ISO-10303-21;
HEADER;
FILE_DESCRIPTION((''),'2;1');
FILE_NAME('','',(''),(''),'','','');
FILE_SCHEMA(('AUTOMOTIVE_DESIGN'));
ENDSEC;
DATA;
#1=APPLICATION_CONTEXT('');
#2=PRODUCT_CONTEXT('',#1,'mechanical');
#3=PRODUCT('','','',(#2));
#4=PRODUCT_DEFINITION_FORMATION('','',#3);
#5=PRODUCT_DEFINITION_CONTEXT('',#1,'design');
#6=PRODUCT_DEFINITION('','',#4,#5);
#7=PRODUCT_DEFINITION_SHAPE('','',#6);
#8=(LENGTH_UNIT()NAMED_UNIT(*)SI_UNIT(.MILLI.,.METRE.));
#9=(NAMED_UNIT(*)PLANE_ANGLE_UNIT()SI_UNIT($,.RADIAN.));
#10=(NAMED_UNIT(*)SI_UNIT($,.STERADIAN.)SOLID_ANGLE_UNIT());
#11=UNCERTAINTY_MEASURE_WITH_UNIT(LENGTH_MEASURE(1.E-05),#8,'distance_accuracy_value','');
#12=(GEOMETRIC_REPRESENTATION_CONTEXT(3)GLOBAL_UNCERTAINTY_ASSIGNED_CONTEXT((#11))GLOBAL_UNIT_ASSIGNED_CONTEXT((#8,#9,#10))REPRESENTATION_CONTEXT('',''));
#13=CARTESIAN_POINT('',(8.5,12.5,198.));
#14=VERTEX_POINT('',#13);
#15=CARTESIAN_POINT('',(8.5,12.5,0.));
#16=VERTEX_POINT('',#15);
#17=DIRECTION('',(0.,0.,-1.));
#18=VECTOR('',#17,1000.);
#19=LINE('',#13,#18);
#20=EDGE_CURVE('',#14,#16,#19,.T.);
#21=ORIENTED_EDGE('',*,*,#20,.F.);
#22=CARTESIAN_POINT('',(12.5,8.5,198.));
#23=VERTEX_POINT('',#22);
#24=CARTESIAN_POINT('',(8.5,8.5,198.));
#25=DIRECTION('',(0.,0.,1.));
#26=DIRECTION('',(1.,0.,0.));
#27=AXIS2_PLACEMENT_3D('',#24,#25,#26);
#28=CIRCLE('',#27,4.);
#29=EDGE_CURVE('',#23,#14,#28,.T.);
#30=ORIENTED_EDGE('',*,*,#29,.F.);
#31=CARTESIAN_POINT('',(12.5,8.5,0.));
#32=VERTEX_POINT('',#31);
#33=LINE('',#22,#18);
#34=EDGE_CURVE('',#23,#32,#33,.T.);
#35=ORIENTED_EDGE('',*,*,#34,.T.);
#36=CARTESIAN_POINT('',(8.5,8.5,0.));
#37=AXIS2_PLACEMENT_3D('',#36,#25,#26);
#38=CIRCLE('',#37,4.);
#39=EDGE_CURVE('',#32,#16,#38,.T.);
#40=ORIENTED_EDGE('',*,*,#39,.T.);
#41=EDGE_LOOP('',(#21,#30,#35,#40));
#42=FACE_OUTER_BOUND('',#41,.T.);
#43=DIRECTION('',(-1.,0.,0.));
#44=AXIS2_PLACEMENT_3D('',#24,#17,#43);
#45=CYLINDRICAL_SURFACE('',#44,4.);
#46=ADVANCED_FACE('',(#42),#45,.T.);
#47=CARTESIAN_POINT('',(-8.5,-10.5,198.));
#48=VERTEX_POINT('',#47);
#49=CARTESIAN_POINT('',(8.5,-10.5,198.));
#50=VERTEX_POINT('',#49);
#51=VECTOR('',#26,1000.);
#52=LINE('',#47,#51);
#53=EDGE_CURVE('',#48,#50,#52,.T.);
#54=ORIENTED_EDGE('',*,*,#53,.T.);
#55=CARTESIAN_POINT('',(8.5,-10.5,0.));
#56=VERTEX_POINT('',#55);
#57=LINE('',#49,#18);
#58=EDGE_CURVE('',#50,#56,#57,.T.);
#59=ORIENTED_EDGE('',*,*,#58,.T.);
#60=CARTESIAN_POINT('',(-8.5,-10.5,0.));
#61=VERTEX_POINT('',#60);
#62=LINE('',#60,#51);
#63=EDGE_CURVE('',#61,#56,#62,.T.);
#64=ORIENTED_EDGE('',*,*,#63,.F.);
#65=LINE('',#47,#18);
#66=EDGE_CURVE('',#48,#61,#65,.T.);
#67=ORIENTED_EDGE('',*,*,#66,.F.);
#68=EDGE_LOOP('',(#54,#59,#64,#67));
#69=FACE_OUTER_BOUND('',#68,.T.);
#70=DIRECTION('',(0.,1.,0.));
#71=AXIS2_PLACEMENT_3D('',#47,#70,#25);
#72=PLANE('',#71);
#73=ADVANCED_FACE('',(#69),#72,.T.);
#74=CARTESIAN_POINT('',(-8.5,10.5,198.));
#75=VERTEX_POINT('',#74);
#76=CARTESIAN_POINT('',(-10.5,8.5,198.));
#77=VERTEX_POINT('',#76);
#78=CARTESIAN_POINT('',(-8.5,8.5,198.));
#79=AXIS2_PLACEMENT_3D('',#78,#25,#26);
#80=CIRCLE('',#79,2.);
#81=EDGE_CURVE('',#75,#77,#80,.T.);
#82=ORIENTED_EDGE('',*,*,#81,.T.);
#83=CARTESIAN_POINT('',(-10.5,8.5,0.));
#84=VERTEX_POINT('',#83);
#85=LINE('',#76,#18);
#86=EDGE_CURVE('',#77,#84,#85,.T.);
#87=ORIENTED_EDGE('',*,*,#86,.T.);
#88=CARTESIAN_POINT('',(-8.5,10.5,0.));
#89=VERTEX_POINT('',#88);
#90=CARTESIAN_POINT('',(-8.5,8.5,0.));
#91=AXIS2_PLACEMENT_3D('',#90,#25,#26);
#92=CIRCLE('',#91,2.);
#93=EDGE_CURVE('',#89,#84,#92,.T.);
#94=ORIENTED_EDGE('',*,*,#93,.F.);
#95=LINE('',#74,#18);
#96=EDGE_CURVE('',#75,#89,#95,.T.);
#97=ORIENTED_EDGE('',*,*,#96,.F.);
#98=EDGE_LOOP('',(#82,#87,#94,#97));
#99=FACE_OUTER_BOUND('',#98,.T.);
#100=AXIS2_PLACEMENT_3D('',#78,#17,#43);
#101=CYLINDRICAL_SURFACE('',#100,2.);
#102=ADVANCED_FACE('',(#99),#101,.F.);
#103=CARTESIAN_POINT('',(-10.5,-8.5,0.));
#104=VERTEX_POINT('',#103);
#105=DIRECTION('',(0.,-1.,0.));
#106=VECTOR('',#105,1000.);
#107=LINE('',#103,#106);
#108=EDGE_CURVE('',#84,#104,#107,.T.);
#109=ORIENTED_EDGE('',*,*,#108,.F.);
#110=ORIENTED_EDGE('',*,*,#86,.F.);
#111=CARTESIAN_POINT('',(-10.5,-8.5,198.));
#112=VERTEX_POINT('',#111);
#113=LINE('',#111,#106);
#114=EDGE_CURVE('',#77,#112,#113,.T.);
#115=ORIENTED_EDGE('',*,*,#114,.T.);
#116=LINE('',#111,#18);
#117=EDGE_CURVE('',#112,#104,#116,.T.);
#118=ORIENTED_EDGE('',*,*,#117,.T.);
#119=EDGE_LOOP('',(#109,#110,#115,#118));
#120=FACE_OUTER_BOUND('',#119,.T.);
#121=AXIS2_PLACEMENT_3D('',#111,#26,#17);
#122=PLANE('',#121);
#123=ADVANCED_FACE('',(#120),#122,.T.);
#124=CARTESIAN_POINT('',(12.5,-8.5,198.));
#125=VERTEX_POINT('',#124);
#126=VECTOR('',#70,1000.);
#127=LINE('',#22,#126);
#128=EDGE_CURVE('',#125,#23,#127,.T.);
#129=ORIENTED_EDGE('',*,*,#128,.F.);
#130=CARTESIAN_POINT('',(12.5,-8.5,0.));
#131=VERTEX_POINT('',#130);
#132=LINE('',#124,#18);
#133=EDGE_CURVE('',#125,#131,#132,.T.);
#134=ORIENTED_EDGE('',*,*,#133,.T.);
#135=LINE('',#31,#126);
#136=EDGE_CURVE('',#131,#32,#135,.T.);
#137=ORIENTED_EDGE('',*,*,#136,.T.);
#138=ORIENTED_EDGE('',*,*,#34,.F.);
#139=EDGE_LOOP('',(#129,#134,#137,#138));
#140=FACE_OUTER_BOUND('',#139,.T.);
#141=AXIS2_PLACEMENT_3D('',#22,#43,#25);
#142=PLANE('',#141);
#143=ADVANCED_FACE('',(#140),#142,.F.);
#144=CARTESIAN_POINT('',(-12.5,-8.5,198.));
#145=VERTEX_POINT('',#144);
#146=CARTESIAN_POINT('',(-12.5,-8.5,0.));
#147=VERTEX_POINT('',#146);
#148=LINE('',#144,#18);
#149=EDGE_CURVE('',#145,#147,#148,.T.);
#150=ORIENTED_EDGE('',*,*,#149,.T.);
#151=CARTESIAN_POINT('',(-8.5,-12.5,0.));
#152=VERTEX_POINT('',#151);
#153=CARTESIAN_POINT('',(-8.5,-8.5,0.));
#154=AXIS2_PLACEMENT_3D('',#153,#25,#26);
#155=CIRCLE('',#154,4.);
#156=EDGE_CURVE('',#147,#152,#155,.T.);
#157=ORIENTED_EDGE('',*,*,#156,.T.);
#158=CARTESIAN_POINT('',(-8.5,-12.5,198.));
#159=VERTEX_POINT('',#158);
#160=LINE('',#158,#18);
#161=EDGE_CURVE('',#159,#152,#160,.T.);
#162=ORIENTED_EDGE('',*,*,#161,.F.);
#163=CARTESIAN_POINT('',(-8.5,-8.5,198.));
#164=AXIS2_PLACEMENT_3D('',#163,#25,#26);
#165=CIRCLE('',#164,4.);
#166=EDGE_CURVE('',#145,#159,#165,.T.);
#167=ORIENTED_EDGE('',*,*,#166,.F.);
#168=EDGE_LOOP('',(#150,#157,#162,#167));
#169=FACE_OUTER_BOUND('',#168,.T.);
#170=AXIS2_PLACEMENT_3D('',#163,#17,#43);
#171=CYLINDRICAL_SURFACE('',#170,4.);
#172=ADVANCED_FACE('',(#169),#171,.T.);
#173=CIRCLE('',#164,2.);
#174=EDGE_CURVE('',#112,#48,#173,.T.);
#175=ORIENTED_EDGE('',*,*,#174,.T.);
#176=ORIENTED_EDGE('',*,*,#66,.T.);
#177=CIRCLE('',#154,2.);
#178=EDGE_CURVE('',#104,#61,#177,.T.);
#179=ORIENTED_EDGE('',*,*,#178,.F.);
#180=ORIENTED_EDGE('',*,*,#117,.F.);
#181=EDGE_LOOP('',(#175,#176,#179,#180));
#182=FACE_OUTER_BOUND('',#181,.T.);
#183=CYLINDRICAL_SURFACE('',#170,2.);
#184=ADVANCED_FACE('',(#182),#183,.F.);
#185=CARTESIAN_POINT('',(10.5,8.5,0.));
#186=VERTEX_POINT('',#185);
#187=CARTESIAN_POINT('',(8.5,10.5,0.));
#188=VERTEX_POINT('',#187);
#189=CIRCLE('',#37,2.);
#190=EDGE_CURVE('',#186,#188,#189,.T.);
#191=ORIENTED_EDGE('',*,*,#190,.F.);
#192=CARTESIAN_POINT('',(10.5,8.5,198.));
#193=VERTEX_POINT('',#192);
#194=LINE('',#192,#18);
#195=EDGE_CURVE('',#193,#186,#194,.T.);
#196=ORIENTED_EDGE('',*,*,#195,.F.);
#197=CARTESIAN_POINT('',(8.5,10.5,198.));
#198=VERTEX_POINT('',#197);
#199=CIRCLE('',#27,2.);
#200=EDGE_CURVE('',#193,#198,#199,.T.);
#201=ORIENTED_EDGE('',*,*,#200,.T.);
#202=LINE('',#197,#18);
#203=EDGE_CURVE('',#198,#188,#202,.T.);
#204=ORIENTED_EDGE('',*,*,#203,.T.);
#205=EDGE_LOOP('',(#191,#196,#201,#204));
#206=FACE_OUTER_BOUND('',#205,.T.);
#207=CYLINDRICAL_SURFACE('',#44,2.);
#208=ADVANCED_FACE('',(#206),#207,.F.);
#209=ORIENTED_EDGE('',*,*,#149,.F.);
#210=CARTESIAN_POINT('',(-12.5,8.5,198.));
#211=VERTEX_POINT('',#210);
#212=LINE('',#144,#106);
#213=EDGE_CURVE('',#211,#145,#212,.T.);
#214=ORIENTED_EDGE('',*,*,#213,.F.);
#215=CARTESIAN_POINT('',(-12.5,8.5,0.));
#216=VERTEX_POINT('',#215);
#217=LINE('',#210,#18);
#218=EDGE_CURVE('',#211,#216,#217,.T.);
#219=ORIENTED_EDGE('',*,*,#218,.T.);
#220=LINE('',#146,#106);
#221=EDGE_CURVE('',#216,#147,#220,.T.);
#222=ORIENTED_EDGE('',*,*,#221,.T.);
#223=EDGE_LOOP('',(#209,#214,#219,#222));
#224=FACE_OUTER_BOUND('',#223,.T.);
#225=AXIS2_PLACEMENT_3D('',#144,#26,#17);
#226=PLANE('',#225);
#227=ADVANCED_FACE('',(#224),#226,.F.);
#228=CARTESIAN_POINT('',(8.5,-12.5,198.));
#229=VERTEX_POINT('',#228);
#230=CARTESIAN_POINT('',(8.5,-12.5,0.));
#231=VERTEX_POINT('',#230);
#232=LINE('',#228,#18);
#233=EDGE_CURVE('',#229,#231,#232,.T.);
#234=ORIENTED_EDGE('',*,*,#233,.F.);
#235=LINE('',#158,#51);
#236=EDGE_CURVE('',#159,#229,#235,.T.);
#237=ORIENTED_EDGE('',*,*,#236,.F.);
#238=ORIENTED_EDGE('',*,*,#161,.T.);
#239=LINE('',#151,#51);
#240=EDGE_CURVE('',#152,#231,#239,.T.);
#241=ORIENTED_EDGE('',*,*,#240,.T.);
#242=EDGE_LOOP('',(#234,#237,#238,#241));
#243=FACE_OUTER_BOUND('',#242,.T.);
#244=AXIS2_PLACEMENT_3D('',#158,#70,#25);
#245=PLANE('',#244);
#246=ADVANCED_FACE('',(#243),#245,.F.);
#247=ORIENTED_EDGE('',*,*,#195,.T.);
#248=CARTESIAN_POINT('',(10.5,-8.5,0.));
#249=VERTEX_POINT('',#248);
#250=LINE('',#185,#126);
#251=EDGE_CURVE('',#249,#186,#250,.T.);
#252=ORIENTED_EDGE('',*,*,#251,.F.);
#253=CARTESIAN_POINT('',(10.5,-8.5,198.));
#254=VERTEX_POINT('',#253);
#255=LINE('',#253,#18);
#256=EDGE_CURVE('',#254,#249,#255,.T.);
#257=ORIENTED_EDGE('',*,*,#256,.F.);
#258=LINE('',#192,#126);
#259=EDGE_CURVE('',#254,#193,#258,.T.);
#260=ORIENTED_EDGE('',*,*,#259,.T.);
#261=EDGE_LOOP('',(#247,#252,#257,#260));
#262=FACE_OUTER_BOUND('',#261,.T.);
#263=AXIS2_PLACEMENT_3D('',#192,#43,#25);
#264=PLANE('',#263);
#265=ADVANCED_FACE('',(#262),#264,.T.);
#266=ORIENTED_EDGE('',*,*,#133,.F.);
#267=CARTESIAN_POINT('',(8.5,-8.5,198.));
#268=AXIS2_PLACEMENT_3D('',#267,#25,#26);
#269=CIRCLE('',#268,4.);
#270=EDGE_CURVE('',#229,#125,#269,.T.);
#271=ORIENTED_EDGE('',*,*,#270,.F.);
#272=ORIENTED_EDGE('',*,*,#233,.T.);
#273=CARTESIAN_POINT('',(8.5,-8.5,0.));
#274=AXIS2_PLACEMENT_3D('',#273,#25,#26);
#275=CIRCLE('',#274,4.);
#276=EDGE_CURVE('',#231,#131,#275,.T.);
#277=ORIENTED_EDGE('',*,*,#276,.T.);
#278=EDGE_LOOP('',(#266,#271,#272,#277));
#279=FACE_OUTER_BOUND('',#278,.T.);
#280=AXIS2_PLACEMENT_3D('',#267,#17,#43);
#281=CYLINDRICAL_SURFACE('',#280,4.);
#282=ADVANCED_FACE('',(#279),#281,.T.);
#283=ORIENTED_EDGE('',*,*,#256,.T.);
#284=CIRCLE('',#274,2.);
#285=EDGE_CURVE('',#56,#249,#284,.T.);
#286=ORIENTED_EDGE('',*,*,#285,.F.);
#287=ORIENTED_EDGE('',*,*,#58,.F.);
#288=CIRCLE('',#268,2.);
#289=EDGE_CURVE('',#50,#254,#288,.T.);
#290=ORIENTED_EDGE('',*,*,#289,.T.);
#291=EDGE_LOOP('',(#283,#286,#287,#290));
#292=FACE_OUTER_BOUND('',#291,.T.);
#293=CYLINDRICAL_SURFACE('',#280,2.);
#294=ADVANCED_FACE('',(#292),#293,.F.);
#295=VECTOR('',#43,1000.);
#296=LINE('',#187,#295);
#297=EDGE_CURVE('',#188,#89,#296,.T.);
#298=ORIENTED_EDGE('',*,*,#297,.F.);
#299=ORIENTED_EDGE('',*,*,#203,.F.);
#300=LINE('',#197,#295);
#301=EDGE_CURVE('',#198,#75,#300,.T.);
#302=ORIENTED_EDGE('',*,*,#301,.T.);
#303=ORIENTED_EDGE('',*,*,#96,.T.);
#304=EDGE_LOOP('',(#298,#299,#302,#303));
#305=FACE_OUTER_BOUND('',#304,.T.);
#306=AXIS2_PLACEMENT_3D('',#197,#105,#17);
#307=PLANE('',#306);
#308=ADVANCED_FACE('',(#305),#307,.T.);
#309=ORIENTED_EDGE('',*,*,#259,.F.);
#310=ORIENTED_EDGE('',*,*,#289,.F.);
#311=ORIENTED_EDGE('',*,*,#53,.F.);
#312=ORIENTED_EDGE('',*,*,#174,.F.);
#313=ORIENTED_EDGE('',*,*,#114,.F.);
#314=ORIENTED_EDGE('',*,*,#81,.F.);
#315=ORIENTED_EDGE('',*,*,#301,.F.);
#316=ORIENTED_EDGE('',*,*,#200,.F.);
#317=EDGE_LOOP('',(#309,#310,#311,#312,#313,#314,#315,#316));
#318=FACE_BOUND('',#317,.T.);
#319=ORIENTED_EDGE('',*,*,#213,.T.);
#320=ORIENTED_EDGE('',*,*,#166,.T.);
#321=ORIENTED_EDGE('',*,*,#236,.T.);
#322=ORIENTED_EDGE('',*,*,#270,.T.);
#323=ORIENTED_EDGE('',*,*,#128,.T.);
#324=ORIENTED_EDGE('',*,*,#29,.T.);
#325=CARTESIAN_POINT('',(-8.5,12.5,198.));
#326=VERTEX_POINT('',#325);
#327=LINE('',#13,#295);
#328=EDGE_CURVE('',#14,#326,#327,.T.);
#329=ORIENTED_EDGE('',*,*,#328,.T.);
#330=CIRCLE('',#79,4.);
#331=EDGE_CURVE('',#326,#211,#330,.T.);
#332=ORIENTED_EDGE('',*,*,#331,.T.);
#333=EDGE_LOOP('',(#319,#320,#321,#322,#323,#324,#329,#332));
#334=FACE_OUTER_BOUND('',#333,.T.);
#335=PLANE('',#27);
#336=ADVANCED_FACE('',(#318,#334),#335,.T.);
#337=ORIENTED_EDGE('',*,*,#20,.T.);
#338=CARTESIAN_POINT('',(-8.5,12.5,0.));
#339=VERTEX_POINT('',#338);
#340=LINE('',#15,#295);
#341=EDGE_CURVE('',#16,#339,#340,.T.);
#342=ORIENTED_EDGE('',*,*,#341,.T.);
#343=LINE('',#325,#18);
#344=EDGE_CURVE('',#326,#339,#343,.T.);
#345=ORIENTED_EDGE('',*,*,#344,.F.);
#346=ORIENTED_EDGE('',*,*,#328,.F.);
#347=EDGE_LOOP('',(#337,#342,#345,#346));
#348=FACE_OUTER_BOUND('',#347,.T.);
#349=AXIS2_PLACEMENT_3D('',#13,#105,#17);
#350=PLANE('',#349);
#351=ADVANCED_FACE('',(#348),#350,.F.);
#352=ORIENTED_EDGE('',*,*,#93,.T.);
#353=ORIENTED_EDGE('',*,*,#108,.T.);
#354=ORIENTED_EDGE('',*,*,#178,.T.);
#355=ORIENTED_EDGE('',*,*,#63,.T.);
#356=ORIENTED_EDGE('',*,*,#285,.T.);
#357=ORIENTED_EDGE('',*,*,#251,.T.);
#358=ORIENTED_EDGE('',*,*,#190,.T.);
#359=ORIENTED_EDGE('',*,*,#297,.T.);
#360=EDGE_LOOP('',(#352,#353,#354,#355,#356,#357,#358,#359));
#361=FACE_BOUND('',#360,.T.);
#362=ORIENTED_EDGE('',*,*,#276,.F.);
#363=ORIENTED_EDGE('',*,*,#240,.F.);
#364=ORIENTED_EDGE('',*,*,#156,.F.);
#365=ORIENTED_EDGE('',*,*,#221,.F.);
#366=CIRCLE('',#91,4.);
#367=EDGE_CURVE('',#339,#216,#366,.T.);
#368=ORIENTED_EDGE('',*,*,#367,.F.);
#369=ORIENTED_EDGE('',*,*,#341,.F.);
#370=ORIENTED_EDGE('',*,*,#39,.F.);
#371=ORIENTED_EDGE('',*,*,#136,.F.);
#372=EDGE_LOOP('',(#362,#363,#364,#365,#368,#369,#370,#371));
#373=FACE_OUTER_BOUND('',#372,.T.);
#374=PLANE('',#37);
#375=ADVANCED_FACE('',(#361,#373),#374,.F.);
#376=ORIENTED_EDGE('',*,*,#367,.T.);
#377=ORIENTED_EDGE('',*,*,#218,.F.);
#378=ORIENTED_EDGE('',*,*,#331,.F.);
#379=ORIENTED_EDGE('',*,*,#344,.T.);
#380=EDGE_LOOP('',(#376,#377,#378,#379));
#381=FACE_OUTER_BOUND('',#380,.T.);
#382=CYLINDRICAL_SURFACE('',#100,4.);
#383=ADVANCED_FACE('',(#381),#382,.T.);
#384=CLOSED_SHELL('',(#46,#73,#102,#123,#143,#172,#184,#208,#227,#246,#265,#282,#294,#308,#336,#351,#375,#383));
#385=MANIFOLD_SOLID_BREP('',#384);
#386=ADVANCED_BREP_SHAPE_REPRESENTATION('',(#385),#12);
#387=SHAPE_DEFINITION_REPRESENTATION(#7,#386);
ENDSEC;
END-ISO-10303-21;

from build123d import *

# Parameters (mm, degrees)
BOSS_EXTRUDE1_DEPTH = 198


with BuildPart() as part:
    # Sketch1 → Boss-Extrude1 (new body)
    with BuildSketch(Plane.XY):
        with BuildLine():
            Line((-8.5, -12.5), (8.5, -12.5))
            ThreePointArc((8.5, -12.5), (11.328427125, -11.328427125), (12.5, -8.5))
            Line((12.5, -8.5), (12.5, 8.5))
            ThreePointArc((12.5, 8.5), (11.328427125, 11.328427125), (8.5, 12.5))
            Line((8.5, 12.5), (-8.5, 12.5))
            ThreePointArc((-8.5, 12.5), (-11.328427125, 11.328427125), (-12.5, 8.5))
            Line((-12.5, 8.5), (-12.5, -8.5))
            ThreePointArc((-12.5, -8.5), (-11.328427125, -11.328427125), (-8.5, -12.5))
        make_face()
        with BuildLine():
            Line((-8.5, -10.5), (8.5, -10.5))
            ThreePointArc((8.5, -10.5), (9.914213562, -9.914213562), (10.5, -8.5))
            Line((10.5, -8.5), (10.5, 8.5))
            ThreePointArc((10.5, 8.5), (9.914213562, 9.914213562), (8.5, 10.5))
            Line((8.5, 10.5), (-8.5, 10.5))
            ThreePointArc((-8.5, 10.5), (-9.914213562, 9.914213562), (-10.5, 8.5))
            Line((-10.5, 8.5), (-10.5, -8.5))
            ThreePointArc((-10.5, -8.5), (-9.914213562, -9.914213562), (-8.5, -10.5))
        make_face(mode=Mode.SUBTRACT)
    extrude(amount=BOSS_EXTRUDE1_DEPTH)


solid = part.part
